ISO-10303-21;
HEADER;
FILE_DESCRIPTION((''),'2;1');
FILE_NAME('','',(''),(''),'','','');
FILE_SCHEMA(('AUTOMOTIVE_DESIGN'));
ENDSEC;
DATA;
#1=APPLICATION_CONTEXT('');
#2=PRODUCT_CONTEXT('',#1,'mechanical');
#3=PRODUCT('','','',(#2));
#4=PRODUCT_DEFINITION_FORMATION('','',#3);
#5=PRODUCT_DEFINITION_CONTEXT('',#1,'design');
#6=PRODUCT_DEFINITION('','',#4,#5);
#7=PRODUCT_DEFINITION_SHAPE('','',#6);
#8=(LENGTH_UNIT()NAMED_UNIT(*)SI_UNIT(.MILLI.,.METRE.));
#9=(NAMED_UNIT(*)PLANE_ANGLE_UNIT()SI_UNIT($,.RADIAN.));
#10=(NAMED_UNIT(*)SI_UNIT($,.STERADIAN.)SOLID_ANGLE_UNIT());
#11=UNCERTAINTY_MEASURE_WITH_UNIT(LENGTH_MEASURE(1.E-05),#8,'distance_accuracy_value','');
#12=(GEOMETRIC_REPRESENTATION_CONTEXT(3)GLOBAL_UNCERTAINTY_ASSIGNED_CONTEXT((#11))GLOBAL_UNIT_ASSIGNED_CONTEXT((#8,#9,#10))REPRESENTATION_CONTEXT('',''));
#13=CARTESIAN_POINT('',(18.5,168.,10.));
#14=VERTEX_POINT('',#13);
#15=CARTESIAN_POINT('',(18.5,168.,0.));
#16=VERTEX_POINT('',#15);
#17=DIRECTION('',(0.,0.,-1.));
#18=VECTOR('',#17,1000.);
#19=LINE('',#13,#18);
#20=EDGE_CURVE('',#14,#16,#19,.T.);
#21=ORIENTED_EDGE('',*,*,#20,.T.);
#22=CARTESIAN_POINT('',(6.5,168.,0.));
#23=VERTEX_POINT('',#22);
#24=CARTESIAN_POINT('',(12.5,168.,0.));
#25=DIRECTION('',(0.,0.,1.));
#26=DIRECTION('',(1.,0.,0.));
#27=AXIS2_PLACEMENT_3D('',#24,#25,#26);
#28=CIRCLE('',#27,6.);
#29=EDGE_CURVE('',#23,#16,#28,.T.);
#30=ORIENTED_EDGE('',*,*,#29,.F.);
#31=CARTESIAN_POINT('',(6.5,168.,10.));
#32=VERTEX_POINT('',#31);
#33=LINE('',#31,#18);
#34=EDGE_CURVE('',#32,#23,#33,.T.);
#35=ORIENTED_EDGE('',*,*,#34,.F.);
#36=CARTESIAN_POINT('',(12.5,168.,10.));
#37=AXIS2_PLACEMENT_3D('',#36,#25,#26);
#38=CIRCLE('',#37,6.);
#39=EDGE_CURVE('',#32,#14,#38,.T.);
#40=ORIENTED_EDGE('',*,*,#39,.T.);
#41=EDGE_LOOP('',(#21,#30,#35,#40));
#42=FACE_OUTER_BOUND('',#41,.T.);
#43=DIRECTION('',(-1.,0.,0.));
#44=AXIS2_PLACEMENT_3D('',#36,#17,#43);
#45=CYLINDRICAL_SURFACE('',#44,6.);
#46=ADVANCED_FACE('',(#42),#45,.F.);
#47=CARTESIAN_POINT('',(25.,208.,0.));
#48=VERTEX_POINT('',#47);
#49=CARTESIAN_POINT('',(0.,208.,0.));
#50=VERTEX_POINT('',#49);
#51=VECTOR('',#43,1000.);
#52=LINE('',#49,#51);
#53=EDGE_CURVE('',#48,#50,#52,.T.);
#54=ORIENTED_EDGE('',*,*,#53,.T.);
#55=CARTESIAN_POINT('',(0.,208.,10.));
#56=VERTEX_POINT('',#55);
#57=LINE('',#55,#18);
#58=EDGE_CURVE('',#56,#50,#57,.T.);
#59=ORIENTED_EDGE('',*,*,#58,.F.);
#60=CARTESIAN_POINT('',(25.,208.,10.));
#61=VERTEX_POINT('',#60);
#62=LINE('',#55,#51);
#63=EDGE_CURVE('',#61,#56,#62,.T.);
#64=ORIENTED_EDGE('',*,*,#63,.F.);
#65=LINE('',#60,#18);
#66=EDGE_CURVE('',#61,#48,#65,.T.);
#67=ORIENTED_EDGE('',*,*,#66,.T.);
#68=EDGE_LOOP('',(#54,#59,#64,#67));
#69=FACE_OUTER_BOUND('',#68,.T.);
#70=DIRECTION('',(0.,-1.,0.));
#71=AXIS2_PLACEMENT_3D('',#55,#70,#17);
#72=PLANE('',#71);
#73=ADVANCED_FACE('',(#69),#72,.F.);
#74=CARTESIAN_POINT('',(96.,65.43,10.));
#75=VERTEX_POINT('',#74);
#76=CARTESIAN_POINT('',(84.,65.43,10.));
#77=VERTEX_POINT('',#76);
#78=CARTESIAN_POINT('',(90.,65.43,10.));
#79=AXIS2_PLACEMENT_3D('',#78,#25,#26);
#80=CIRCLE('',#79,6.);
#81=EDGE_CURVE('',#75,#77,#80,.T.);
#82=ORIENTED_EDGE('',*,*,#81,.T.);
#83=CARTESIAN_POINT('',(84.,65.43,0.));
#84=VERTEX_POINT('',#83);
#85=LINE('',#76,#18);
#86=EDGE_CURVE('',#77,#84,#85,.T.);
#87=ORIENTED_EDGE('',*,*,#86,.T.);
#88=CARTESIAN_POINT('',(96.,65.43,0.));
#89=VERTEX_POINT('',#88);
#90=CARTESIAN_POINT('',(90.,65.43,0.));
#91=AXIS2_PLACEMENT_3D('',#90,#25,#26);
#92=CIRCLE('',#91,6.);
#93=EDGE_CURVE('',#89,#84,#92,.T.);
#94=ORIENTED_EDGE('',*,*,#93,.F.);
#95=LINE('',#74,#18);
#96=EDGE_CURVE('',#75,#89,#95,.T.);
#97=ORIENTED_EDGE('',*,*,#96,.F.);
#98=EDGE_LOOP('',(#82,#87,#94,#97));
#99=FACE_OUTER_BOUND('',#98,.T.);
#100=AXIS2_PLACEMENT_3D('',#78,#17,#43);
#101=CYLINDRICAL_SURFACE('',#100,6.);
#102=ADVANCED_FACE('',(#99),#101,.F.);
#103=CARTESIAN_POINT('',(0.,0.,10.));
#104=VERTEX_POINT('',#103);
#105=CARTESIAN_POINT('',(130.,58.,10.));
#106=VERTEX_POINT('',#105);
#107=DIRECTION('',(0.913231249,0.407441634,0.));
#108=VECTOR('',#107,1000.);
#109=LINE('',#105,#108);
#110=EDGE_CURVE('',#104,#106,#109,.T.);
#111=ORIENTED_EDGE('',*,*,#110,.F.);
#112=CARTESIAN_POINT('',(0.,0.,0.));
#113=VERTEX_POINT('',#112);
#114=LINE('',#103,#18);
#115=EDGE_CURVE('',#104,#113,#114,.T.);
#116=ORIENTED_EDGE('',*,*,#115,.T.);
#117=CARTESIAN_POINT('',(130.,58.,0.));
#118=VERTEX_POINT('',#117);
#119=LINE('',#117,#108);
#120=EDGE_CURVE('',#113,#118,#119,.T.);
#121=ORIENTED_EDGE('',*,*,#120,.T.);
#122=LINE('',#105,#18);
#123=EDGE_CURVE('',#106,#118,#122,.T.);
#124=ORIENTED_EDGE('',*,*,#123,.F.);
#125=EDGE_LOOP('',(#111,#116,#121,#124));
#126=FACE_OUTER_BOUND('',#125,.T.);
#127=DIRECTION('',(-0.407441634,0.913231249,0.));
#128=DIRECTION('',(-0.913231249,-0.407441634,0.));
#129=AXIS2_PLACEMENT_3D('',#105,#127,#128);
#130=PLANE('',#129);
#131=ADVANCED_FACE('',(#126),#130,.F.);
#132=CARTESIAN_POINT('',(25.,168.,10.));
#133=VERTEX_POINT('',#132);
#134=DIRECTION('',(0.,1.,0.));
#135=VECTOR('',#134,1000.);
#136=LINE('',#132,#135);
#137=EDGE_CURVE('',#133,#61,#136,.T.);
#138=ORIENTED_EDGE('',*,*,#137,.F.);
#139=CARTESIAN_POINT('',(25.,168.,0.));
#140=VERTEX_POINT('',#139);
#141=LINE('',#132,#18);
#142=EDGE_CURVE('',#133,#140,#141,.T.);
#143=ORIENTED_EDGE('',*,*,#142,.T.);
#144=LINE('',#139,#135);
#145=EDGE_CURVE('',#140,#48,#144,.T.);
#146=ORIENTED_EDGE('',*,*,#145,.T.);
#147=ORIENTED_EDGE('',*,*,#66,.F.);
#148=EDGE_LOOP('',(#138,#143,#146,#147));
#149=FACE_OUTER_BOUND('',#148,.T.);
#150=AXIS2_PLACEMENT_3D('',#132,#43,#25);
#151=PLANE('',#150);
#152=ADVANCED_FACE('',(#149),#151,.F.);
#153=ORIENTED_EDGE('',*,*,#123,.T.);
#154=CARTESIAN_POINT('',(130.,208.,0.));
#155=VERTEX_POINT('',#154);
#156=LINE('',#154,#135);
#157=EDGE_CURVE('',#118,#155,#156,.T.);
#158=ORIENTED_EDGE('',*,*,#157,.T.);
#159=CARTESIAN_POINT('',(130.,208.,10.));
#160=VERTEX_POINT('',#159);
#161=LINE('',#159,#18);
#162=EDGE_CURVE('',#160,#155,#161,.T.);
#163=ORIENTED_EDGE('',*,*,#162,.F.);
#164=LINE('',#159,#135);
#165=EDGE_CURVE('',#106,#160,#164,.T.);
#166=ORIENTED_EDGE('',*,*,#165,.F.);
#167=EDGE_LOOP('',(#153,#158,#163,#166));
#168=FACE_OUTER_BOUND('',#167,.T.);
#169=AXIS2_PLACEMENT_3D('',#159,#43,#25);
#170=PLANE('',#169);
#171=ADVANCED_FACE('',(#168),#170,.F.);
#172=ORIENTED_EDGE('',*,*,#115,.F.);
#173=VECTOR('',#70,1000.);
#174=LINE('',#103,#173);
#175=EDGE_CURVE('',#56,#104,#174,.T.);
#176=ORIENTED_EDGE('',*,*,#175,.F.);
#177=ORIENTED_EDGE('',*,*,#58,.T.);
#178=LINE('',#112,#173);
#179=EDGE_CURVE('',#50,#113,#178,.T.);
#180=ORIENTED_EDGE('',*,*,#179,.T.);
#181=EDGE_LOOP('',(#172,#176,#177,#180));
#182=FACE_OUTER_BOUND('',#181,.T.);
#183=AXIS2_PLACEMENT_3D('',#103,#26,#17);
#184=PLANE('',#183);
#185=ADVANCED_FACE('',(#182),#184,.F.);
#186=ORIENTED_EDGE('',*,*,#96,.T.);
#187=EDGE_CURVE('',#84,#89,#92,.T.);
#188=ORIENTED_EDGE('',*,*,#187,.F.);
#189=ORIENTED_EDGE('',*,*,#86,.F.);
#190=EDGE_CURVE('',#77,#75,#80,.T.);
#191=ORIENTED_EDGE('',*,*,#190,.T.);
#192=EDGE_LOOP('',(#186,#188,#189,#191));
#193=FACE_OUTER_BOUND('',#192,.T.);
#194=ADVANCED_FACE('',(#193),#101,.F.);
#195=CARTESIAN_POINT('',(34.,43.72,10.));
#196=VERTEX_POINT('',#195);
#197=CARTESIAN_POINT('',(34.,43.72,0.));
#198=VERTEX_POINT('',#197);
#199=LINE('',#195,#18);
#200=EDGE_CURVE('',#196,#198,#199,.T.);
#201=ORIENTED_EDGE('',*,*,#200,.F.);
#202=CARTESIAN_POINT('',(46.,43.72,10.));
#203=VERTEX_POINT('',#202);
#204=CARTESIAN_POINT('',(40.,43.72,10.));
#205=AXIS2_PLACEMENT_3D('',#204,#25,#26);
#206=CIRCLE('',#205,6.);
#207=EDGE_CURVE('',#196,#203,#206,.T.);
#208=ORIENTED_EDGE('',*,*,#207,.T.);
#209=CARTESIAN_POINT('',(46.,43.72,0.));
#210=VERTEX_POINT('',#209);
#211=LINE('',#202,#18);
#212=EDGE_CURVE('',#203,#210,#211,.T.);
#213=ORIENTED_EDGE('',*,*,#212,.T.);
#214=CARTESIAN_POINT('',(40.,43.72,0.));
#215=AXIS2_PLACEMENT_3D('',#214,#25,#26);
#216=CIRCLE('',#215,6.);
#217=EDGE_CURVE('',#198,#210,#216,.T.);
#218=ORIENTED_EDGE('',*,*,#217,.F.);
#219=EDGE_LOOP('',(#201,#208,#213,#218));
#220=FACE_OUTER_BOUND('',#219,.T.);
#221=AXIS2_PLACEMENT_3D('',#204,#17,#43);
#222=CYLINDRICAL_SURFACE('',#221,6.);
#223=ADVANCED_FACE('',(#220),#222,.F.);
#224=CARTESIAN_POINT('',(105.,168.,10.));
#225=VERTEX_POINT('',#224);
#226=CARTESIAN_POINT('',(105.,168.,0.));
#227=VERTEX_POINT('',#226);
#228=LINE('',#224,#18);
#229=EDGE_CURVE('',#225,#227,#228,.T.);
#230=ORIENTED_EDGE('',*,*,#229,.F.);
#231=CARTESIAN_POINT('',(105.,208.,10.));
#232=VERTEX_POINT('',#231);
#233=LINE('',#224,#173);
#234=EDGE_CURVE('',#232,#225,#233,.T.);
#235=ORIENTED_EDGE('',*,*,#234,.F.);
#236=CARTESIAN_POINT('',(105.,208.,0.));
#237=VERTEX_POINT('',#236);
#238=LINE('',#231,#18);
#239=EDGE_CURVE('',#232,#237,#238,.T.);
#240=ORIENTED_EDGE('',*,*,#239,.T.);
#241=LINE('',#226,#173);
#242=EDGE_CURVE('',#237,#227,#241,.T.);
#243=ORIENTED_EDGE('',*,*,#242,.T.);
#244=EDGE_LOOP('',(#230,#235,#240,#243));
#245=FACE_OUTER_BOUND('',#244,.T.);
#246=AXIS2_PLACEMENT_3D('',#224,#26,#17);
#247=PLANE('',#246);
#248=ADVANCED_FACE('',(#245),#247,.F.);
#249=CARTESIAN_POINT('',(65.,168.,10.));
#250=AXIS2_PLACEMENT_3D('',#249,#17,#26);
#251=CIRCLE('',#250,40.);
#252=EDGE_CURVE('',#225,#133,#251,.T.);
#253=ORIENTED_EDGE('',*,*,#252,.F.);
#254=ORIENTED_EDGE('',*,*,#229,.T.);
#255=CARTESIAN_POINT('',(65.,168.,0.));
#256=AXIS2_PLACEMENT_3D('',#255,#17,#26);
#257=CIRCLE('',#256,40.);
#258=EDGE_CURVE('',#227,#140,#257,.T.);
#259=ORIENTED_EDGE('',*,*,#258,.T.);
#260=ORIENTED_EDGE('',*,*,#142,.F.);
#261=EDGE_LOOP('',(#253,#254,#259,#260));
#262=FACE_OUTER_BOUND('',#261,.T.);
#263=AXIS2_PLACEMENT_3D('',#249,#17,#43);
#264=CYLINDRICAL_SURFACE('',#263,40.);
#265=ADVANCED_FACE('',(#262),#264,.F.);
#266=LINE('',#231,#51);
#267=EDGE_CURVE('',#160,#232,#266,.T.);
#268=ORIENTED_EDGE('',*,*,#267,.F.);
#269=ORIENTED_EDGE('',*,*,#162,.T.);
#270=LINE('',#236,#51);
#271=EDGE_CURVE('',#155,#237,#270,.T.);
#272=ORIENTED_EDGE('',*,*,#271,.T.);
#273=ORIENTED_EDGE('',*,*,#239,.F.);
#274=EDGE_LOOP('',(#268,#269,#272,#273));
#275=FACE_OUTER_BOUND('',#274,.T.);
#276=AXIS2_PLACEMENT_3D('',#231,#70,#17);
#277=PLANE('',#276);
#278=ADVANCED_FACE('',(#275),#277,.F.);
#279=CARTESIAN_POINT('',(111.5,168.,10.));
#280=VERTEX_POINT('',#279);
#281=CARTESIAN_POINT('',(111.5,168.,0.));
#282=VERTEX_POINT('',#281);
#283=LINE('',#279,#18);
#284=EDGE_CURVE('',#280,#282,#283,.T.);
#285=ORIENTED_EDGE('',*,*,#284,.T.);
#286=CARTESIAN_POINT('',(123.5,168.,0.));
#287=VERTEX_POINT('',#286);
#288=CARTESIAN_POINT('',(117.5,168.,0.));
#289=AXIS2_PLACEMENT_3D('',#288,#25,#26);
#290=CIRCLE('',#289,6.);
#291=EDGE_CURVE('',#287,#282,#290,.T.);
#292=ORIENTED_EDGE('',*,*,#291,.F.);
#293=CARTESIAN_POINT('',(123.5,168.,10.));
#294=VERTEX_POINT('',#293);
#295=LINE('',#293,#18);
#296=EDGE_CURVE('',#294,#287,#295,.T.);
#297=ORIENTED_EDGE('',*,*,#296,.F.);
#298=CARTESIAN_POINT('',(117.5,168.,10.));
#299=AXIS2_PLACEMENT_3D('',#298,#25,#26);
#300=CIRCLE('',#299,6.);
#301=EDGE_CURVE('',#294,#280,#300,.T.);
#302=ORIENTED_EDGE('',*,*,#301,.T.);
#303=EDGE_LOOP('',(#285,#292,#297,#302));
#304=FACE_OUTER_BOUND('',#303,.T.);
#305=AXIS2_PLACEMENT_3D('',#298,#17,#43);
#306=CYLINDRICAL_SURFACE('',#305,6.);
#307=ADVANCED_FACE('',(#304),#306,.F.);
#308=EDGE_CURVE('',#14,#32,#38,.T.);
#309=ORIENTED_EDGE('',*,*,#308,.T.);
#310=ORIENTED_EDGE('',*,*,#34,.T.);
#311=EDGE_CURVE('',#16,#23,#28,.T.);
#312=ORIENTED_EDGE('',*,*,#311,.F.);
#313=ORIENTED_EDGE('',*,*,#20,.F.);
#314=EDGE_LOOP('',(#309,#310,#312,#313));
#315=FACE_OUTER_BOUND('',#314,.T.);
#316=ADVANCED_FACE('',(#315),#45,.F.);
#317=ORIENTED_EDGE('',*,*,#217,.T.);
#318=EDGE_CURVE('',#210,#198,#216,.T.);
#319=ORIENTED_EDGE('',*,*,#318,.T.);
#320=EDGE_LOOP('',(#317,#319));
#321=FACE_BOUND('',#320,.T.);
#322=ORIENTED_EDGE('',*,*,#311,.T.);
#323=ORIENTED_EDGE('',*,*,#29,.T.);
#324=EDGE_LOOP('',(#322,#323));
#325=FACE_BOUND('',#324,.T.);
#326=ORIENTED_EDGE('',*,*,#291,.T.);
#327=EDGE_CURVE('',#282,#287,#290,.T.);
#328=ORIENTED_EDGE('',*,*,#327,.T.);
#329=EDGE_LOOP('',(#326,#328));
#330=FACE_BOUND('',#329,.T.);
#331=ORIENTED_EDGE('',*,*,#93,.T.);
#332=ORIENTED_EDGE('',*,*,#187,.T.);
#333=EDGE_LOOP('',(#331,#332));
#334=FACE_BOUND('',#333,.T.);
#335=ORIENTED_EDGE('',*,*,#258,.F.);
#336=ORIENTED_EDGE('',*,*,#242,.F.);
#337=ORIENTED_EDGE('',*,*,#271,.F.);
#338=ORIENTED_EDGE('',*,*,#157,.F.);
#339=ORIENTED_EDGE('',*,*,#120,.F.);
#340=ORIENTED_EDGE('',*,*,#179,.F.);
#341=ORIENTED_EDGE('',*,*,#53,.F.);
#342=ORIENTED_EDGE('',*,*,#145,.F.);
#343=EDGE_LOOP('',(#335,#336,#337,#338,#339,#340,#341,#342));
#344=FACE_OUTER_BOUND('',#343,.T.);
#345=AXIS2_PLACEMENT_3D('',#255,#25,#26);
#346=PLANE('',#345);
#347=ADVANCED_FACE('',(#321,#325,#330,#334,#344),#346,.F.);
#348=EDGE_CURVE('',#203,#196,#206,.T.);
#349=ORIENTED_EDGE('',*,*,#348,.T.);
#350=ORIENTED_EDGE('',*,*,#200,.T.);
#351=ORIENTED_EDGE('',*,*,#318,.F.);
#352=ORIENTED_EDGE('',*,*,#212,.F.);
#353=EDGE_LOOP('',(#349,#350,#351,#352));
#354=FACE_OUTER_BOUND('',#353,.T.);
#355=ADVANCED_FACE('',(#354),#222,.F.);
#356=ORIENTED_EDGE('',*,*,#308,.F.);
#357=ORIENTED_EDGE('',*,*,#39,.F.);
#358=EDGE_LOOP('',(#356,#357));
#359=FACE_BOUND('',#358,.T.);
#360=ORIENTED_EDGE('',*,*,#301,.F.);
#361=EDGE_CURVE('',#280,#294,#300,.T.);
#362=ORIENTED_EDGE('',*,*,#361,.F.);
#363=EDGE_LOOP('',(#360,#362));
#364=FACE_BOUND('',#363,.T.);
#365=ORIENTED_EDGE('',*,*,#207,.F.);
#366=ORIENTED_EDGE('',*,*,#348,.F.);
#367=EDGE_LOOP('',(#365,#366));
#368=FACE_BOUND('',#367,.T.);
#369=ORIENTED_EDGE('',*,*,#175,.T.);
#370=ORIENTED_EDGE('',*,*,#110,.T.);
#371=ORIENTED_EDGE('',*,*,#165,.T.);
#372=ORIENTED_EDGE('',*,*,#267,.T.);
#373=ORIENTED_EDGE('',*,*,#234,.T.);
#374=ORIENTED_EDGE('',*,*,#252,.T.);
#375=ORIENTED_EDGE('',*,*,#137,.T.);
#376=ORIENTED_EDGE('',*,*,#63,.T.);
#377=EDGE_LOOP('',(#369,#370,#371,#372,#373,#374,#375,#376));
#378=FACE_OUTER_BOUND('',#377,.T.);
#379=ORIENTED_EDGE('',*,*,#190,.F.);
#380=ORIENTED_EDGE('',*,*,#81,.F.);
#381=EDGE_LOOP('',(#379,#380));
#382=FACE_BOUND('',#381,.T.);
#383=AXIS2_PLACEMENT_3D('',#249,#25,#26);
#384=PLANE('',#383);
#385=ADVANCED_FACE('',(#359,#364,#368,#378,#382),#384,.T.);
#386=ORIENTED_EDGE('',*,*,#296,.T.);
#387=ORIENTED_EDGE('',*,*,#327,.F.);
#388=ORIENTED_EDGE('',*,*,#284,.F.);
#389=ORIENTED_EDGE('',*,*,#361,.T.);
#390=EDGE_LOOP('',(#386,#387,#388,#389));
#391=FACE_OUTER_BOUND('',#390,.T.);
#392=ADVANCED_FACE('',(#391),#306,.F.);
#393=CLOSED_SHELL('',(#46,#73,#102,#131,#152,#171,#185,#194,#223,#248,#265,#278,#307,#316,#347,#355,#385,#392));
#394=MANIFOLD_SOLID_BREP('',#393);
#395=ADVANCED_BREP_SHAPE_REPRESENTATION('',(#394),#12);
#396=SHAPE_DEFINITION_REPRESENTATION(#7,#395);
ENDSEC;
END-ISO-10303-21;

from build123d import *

# Parameters (mm, degrees)
SKETCH_1_R      = 6
EXTRUDE_1_DEPTH = 10


with BuildPart() as part:
    # 草图1 → 凸台-拉伸1 (new body)
    with BuildSketch(Plane.XY):
        with BuildLine():
            Line((130, 208), (130, 58))
            Line((130, 58), (0, 0))
            Line((0, 0), (0, 208))
            Line((0, 208), (25, 208))
            Line((25, 208), (25, 168))
            ThreePointArc((25, 168), (65, 128), (105, 168))
            Line((105, 168), (105, 208))
            Line((105, 208), (130, 208))
        make_face()
        with Locations((117.5, 168)):
            Circle(SKETCH_1_R, mode=Mode.SUBTRACT)
        with Locations((12.5, 168)):
            Circle(SKETCH_1_R, mode=Mode.SUBTRACT)
        with Locations((40, 43.72)):
            Circle(SKETCH_1_R, mode=Mode.SUBTRACT)
        with Locations((90, 65.43)):
            Circle(SKETCH_1_R, mode=Mode.SUBTRACT)
    extrude(amount=EXTRUDE_1_DEPTH)


solid = part.part
